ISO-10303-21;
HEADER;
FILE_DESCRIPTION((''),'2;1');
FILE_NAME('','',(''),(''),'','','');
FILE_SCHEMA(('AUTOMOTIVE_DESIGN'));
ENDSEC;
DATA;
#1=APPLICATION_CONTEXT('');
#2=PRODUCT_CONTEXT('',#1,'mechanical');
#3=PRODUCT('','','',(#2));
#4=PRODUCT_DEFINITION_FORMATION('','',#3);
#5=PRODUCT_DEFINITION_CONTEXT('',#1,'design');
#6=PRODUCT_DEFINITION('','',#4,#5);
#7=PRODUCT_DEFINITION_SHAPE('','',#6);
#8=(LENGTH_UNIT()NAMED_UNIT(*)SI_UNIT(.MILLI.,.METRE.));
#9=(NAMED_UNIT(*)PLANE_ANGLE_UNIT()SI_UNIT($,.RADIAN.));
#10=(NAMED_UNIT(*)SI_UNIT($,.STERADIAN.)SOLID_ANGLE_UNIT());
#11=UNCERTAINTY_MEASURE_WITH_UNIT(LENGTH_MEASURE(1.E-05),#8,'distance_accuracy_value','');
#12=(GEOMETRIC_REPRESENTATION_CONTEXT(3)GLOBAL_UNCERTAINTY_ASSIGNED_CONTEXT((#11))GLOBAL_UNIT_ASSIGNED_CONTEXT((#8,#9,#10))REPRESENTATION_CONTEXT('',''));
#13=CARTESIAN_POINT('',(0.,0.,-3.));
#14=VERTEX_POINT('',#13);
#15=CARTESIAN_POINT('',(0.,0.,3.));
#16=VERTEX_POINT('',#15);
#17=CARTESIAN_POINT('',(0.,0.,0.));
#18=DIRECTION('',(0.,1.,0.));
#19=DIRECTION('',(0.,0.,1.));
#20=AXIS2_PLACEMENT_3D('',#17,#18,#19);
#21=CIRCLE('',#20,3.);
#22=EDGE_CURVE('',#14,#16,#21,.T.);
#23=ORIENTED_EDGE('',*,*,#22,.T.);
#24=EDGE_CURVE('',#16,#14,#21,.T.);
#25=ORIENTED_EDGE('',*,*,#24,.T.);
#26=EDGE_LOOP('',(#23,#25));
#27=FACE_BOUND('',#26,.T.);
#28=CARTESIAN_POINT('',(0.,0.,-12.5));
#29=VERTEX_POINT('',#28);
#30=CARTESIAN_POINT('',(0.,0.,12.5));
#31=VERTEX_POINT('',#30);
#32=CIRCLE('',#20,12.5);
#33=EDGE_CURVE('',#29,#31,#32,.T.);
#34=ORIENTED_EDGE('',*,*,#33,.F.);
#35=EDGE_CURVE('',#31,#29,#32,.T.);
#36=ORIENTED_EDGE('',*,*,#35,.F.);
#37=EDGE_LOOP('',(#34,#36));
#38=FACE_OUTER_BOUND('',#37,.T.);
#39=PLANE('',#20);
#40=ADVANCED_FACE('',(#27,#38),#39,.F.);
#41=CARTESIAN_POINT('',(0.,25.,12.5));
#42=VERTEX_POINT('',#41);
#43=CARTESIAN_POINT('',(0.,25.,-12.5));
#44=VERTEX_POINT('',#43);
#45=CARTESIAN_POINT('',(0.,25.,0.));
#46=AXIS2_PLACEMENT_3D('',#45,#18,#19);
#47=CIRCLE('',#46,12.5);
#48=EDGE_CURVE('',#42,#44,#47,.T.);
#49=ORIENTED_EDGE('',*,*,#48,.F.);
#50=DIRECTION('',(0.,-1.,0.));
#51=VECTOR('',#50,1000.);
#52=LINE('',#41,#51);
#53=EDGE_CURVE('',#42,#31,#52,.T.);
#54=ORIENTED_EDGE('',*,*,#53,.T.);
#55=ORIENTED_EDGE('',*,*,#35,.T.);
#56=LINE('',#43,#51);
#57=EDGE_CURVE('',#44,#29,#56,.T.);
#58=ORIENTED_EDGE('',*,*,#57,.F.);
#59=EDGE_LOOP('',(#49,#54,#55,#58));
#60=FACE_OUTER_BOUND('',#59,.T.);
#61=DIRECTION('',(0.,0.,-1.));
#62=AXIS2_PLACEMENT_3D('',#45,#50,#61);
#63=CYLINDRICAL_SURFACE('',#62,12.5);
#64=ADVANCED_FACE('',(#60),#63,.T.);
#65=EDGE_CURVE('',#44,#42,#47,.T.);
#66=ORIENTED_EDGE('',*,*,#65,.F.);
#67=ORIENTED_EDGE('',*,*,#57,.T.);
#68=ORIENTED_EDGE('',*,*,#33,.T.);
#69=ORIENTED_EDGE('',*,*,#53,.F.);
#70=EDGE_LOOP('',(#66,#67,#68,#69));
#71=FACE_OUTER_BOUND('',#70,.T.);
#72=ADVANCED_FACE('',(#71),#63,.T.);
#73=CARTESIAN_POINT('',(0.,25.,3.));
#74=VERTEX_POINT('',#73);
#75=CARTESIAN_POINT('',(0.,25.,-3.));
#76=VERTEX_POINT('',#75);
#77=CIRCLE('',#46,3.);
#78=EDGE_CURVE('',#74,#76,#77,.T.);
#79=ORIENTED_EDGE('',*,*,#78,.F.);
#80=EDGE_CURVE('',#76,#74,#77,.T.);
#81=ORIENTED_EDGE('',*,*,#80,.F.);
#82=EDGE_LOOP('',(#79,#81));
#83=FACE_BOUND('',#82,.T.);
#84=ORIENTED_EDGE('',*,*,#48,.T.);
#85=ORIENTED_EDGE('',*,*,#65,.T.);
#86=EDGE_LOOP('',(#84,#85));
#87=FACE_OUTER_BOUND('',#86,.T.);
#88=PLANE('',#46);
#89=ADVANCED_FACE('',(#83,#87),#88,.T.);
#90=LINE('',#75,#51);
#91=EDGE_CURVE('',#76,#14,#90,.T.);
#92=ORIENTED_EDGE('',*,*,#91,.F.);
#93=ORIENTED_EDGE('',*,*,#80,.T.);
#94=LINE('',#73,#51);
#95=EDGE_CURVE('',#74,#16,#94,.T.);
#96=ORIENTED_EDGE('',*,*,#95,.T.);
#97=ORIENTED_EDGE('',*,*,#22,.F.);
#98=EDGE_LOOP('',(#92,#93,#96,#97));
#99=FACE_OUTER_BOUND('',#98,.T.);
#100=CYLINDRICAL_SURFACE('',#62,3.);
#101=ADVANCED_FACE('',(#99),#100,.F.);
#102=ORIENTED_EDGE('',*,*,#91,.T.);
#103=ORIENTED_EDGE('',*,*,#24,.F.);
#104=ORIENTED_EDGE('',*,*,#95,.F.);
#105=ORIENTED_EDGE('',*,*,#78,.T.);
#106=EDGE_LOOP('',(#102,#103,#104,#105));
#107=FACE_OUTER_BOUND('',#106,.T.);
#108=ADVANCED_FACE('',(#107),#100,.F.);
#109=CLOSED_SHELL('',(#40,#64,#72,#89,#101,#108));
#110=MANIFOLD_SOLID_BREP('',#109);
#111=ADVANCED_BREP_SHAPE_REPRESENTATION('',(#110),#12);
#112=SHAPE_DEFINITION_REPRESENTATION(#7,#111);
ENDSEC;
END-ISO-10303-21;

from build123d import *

# Parameters (mm, degrees)
SKETCH1_R           = 12.5
SKETCH1_R_2         = 3
BOSS_EXTRUDE1_DEPTH = 25


with BuildPart() as part:
    # Sketch1 → Boss-Extrude1 (new body)
    with BuildSketch(Plane(origin=(0, 0, 0), x_dir=(1, 0, 0), z_dir=(0, 1, 0))):
        with Locations(Location((0, 0, 0), (0, 0, 270))):
            Circle(SKETCH1_R)
        with Locations(Location((0, 0, 0), (0, 0, 270))):
            Circle(SKETCH1_R_2, mode=Mode.SUBTRACT)
    extrude(amount=BOSS_EXTRUDE1_DEPTH)


solid = part.part
